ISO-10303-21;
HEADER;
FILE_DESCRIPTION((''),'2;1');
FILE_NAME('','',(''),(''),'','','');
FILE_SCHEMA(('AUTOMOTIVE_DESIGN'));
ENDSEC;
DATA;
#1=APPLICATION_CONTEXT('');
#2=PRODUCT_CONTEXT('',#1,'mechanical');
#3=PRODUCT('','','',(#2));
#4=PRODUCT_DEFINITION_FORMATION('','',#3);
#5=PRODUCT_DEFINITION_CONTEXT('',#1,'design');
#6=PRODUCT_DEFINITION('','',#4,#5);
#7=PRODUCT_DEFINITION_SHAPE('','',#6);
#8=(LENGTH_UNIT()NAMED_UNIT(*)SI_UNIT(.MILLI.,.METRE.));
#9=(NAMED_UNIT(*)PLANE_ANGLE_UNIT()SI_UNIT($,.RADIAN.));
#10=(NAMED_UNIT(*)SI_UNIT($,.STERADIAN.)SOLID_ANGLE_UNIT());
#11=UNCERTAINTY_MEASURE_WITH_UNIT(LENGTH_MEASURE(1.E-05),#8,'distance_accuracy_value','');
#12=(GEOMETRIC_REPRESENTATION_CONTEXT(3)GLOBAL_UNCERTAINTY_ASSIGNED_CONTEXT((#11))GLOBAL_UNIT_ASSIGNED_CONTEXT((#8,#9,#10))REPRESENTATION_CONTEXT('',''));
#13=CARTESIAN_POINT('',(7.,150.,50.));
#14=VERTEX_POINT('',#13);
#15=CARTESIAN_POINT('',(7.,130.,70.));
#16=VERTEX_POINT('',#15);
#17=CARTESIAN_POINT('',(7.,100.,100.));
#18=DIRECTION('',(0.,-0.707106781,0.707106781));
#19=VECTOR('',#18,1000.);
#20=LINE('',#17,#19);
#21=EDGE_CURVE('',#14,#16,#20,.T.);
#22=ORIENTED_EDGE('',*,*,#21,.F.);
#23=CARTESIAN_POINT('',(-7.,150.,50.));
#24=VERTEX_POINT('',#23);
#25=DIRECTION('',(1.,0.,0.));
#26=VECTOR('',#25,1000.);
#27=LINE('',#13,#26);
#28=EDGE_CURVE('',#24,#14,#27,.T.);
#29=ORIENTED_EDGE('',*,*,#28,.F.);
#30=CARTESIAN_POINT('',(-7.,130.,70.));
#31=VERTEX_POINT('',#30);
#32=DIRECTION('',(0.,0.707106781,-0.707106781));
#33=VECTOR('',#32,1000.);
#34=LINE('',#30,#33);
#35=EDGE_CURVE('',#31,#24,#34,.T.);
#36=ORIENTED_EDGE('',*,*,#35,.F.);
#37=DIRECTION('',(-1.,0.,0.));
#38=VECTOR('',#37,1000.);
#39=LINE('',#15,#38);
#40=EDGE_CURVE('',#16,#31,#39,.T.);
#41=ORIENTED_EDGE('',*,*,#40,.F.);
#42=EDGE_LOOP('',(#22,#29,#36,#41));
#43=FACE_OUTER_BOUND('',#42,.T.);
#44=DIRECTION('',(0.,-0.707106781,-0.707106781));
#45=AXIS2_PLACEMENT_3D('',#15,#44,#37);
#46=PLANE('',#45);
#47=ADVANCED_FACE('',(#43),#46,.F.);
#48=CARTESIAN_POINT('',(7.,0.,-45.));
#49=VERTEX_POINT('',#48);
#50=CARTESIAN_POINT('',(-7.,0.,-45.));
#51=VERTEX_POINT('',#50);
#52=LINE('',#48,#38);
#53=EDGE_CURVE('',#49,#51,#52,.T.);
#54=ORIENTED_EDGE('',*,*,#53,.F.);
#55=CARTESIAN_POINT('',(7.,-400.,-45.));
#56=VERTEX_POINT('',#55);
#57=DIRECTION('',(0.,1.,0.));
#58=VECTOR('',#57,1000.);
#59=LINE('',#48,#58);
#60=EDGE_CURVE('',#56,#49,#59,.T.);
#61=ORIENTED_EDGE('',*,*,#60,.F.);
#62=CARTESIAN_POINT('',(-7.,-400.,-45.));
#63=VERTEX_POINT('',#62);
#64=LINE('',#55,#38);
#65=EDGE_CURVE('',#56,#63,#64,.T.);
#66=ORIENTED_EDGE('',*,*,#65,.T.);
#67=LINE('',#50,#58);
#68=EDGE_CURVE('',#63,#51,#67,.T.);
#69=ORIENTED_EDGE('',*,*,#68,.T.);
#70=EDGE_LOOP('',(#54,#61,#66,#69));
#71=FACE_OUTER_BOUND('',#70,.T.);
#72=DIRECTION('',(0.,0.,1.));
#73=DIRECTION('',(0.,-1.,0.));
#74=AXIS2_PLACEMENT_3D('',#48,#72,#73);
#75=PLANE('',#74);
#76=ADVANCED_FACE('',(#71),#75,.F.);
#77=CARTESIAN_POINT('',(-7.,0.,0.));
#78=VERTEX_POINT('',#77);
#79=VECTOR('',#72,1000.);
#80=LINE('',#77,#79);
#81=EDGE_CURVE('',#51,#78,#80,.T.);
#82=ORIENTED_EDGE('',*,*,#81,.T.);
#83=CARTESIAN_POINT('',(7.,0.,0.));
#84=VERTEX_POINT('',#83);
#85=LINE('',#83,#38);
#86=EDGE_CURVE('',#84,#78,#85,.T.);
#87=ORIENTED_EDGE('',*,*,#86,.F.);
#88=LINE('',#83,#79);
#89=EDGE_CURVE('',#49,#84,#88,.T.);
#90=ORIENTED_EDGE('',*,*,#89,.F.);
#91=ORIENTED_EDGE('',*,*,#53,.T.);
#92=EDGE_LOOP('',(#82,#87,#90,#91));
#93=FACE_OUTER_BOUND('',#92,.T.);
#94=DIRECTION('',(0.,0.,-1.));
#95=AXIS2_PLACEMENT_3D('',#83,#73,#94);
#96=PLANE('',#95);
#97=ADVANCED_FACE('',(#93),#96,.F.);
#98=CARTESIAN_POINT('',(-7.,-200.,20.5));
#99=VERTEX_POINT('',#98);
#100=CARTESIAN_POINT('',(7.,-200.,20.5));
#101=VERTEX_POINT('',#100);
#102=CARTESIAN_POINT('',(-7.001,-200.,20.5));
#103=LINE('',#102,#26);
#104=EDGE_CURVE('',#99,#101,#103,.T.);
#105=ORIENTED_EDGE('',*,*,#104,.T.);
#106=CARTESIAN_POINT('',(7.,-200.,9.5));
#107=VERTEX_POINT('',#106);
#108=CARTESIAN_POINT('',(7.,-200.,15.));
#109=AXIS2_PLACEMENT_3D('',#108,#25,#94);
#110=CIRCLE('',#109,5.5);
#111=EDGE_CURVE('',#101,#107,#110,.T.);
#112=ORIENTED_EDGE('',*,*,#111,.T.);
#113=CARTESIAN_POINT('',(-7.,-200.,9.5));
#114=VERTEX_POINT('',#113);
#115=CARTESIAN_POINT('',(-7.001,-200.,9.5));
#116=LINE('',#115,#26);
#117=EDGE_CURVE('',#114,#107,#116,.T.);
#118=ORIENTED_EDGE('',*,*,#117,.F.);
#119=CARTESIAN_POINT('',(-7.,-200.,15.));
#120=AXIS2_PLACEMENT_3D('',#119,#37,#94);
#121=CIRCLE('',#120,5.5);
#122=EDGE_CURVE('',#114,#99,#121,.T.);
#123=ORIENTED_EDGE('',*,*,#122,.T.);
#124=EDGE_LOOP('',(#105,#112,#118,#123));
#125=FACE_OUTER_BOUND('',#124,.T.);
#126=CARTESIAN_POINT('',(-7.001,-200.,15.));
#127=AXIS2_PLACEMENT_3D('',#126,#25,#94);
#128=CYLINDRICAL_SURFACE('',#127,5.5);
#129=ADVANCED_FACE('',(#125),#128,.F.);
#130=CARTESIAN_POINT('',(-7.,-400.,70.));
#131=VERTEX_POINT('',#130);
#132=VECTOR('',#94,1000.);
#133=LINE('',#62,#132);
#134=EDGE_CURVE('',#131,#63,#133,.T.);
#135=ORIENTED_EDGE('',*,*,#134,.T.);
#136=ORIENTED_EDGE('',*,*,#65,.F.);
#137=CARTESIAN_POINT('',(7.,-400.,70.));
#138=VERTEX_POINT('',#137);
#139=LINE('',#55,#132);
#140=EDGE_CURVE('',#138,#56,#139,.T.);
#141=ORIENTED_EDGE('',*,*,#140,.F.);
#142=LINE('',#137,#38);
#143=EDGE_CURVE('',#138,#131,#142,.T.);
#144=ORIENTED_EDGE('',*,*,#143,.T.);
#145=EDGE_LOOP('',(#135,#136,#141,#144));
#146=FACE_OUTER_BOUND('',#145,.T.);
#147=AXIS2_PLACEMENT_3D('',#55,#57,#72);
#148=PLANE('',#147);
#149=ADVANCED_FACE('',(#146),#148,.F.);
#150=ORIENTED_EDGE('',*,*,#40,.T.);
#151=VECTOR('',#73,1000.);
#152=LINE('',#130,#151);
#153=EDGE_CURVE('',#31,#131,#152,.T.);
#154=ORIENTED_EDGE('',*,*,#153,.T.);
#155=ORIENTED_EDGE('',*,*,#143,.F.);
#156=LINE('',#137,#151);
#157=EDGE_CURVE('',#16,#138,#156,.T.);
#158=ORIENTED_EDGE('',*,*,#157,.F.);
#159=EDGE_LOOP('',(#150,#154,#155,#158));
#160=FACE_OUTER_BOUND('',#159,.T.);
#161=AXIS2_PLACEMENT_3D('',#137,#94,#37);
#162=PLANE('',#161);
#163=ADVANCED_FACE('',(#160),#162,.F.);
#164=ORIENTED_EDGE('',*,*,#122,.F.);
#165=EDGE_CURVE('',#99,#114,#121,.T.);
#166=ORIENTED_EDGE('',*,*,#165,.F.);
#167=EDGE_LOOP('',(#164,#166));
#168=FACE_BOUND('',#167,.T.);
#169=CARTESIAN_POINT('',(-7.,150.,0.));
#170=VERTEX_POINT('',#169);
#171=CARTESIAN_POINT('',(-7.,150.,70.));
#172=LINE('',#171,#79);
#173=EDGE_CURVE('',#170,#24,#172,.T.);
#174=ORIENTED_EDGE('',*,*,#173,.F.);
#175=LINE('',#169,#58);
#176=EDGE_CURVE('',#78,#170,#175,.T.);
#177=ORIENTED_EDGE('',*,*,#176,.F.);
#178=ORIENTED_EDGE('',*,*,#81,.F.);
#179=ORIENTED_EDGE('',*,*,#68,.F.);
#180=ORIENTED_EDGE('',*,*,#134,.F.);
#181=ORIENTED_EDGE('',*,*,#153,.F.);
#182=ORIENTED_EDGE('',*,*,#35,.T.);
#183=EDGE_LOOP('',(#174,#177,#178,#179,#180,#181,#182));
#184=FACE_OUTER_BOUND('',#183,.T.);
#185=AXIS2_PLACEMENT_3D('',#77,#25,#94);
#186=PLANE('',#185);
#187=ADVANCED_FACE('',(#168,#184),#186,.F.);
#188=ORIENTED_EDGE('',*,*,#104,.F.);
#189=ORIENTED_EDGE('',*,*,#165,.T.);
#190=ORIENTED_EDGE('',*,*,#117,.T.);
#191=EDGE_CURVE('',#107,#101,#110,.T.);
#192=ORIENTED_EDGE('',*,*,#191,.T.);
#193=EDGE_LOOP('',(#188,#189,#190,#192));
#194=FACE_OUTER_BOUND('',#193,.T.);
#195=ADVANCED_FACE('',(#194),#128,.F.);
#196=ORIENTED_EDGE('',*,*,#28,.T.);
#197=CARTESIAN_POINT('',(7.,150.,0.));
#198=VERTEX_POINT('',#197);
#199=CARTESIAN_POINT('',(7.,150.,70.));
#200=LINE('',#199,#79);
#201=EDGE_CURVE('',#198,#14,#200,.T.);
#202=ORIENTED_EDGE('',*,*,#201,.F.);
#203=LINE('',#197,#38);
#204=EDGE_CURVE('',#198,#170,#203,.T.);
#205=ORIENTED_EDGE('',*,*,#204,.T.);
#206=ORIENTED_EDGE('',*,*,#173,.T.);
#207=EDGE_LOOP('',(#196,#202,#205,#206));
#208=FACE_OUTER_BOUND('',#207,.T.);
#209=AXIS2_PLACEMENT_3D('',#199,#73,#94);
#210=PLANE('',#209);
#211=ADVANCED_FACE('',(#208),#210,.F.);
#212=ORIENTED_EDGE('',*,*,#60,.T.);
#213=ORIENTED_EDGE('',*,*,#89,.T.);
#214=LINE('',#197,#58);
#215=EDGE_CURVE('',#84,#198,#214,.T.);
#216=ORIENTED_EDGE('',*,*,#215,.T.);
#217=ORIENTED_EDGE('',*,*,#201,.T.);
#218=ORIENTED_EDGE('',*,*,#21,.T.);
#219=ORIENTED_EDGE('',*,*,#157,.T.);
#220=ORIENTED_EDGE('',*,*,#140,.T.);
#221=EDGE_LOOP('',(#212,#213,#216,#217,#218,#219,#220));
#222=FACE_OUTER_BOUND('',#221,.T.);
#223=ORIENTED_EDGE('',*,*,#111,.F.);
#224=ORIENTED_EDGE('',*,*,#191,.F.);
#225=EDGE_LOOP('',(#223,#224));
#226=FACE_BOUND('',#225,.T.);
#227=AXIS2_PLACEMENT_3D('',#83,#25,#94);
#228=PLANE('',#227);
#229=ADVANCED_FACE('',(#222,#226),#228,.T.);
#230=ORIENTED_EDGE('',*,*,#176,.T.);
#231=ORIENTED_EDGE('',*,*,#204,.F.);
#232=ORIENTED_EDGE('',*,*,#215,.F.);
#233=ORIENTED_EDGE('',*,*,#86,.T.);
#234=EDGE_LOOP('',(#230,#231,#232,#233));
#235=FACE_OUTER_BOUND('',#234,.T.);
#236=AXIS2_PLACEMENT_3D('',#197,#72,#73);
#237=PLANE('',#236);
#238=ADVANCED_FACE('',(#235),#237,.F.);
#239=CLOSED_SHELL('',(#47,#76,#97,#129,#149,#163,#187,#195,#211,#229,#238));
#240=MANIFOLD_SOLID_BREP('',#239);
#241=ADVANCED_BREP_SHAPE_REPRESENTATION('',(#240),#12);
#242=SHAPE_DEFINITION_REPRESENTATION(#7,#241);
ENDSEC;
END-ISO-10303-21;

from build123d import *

# Parameters (mm, degrees)
EXTRUDE_1_DEPTH     = 7
CUT_EXTRUDE_2_REACH = 408.32
SKETCH_3_R          = 5.5
CHAMFER_1_SIZE      = 20


with BuildPart() as part:
    # 草图1 → 凸台-拉伸1 (new, symmetric)
    with BuildSketch(Plane(origin=(0, 0, 0), x_dir=(0, 0, -1), z_dir=(1, 0, 0))):
        Polygon((0, 0), (45, 0), (45, -400), (-70, -400), (-70, 150), (0, 150), align=None)
    extrude(amount=EXTRUDE_1_DEPTH, both=True)

    # 草图3 → 切除-拉伸2 (cut, up to next)
    with BuildSketch(Plane(origin=(7, 0, 0), x_dir=(0, 0, -1), z_dir=(1, 0, 0)), mode=Mode.PRIVATE) as cut_extrude_2_sk1:
        with Locations((-15, -200)):
            Circle(SKETCH_3_R)
    cut_extrude_2_tool1 = extrude(cut_extrude_2_sk1.sketch, amount=-CUT_EXTRUDE_2_REACH, mode=Mode.PRIVATE) & part.part
    add(cut_extrude_2_tool1.solids().sort_by_distance((7, -200, 15))[0], mode=Mode.SUBTRACT)

    # 倒角1
    chamfer_1_edges = [part.edges().sort_by_distance(p)[0] for p in [
        (0, 150, 70),
    ]]
    chamfer(chamfer_1_edges, length=CHAMFER_1_SIZE)


solid = part.part
